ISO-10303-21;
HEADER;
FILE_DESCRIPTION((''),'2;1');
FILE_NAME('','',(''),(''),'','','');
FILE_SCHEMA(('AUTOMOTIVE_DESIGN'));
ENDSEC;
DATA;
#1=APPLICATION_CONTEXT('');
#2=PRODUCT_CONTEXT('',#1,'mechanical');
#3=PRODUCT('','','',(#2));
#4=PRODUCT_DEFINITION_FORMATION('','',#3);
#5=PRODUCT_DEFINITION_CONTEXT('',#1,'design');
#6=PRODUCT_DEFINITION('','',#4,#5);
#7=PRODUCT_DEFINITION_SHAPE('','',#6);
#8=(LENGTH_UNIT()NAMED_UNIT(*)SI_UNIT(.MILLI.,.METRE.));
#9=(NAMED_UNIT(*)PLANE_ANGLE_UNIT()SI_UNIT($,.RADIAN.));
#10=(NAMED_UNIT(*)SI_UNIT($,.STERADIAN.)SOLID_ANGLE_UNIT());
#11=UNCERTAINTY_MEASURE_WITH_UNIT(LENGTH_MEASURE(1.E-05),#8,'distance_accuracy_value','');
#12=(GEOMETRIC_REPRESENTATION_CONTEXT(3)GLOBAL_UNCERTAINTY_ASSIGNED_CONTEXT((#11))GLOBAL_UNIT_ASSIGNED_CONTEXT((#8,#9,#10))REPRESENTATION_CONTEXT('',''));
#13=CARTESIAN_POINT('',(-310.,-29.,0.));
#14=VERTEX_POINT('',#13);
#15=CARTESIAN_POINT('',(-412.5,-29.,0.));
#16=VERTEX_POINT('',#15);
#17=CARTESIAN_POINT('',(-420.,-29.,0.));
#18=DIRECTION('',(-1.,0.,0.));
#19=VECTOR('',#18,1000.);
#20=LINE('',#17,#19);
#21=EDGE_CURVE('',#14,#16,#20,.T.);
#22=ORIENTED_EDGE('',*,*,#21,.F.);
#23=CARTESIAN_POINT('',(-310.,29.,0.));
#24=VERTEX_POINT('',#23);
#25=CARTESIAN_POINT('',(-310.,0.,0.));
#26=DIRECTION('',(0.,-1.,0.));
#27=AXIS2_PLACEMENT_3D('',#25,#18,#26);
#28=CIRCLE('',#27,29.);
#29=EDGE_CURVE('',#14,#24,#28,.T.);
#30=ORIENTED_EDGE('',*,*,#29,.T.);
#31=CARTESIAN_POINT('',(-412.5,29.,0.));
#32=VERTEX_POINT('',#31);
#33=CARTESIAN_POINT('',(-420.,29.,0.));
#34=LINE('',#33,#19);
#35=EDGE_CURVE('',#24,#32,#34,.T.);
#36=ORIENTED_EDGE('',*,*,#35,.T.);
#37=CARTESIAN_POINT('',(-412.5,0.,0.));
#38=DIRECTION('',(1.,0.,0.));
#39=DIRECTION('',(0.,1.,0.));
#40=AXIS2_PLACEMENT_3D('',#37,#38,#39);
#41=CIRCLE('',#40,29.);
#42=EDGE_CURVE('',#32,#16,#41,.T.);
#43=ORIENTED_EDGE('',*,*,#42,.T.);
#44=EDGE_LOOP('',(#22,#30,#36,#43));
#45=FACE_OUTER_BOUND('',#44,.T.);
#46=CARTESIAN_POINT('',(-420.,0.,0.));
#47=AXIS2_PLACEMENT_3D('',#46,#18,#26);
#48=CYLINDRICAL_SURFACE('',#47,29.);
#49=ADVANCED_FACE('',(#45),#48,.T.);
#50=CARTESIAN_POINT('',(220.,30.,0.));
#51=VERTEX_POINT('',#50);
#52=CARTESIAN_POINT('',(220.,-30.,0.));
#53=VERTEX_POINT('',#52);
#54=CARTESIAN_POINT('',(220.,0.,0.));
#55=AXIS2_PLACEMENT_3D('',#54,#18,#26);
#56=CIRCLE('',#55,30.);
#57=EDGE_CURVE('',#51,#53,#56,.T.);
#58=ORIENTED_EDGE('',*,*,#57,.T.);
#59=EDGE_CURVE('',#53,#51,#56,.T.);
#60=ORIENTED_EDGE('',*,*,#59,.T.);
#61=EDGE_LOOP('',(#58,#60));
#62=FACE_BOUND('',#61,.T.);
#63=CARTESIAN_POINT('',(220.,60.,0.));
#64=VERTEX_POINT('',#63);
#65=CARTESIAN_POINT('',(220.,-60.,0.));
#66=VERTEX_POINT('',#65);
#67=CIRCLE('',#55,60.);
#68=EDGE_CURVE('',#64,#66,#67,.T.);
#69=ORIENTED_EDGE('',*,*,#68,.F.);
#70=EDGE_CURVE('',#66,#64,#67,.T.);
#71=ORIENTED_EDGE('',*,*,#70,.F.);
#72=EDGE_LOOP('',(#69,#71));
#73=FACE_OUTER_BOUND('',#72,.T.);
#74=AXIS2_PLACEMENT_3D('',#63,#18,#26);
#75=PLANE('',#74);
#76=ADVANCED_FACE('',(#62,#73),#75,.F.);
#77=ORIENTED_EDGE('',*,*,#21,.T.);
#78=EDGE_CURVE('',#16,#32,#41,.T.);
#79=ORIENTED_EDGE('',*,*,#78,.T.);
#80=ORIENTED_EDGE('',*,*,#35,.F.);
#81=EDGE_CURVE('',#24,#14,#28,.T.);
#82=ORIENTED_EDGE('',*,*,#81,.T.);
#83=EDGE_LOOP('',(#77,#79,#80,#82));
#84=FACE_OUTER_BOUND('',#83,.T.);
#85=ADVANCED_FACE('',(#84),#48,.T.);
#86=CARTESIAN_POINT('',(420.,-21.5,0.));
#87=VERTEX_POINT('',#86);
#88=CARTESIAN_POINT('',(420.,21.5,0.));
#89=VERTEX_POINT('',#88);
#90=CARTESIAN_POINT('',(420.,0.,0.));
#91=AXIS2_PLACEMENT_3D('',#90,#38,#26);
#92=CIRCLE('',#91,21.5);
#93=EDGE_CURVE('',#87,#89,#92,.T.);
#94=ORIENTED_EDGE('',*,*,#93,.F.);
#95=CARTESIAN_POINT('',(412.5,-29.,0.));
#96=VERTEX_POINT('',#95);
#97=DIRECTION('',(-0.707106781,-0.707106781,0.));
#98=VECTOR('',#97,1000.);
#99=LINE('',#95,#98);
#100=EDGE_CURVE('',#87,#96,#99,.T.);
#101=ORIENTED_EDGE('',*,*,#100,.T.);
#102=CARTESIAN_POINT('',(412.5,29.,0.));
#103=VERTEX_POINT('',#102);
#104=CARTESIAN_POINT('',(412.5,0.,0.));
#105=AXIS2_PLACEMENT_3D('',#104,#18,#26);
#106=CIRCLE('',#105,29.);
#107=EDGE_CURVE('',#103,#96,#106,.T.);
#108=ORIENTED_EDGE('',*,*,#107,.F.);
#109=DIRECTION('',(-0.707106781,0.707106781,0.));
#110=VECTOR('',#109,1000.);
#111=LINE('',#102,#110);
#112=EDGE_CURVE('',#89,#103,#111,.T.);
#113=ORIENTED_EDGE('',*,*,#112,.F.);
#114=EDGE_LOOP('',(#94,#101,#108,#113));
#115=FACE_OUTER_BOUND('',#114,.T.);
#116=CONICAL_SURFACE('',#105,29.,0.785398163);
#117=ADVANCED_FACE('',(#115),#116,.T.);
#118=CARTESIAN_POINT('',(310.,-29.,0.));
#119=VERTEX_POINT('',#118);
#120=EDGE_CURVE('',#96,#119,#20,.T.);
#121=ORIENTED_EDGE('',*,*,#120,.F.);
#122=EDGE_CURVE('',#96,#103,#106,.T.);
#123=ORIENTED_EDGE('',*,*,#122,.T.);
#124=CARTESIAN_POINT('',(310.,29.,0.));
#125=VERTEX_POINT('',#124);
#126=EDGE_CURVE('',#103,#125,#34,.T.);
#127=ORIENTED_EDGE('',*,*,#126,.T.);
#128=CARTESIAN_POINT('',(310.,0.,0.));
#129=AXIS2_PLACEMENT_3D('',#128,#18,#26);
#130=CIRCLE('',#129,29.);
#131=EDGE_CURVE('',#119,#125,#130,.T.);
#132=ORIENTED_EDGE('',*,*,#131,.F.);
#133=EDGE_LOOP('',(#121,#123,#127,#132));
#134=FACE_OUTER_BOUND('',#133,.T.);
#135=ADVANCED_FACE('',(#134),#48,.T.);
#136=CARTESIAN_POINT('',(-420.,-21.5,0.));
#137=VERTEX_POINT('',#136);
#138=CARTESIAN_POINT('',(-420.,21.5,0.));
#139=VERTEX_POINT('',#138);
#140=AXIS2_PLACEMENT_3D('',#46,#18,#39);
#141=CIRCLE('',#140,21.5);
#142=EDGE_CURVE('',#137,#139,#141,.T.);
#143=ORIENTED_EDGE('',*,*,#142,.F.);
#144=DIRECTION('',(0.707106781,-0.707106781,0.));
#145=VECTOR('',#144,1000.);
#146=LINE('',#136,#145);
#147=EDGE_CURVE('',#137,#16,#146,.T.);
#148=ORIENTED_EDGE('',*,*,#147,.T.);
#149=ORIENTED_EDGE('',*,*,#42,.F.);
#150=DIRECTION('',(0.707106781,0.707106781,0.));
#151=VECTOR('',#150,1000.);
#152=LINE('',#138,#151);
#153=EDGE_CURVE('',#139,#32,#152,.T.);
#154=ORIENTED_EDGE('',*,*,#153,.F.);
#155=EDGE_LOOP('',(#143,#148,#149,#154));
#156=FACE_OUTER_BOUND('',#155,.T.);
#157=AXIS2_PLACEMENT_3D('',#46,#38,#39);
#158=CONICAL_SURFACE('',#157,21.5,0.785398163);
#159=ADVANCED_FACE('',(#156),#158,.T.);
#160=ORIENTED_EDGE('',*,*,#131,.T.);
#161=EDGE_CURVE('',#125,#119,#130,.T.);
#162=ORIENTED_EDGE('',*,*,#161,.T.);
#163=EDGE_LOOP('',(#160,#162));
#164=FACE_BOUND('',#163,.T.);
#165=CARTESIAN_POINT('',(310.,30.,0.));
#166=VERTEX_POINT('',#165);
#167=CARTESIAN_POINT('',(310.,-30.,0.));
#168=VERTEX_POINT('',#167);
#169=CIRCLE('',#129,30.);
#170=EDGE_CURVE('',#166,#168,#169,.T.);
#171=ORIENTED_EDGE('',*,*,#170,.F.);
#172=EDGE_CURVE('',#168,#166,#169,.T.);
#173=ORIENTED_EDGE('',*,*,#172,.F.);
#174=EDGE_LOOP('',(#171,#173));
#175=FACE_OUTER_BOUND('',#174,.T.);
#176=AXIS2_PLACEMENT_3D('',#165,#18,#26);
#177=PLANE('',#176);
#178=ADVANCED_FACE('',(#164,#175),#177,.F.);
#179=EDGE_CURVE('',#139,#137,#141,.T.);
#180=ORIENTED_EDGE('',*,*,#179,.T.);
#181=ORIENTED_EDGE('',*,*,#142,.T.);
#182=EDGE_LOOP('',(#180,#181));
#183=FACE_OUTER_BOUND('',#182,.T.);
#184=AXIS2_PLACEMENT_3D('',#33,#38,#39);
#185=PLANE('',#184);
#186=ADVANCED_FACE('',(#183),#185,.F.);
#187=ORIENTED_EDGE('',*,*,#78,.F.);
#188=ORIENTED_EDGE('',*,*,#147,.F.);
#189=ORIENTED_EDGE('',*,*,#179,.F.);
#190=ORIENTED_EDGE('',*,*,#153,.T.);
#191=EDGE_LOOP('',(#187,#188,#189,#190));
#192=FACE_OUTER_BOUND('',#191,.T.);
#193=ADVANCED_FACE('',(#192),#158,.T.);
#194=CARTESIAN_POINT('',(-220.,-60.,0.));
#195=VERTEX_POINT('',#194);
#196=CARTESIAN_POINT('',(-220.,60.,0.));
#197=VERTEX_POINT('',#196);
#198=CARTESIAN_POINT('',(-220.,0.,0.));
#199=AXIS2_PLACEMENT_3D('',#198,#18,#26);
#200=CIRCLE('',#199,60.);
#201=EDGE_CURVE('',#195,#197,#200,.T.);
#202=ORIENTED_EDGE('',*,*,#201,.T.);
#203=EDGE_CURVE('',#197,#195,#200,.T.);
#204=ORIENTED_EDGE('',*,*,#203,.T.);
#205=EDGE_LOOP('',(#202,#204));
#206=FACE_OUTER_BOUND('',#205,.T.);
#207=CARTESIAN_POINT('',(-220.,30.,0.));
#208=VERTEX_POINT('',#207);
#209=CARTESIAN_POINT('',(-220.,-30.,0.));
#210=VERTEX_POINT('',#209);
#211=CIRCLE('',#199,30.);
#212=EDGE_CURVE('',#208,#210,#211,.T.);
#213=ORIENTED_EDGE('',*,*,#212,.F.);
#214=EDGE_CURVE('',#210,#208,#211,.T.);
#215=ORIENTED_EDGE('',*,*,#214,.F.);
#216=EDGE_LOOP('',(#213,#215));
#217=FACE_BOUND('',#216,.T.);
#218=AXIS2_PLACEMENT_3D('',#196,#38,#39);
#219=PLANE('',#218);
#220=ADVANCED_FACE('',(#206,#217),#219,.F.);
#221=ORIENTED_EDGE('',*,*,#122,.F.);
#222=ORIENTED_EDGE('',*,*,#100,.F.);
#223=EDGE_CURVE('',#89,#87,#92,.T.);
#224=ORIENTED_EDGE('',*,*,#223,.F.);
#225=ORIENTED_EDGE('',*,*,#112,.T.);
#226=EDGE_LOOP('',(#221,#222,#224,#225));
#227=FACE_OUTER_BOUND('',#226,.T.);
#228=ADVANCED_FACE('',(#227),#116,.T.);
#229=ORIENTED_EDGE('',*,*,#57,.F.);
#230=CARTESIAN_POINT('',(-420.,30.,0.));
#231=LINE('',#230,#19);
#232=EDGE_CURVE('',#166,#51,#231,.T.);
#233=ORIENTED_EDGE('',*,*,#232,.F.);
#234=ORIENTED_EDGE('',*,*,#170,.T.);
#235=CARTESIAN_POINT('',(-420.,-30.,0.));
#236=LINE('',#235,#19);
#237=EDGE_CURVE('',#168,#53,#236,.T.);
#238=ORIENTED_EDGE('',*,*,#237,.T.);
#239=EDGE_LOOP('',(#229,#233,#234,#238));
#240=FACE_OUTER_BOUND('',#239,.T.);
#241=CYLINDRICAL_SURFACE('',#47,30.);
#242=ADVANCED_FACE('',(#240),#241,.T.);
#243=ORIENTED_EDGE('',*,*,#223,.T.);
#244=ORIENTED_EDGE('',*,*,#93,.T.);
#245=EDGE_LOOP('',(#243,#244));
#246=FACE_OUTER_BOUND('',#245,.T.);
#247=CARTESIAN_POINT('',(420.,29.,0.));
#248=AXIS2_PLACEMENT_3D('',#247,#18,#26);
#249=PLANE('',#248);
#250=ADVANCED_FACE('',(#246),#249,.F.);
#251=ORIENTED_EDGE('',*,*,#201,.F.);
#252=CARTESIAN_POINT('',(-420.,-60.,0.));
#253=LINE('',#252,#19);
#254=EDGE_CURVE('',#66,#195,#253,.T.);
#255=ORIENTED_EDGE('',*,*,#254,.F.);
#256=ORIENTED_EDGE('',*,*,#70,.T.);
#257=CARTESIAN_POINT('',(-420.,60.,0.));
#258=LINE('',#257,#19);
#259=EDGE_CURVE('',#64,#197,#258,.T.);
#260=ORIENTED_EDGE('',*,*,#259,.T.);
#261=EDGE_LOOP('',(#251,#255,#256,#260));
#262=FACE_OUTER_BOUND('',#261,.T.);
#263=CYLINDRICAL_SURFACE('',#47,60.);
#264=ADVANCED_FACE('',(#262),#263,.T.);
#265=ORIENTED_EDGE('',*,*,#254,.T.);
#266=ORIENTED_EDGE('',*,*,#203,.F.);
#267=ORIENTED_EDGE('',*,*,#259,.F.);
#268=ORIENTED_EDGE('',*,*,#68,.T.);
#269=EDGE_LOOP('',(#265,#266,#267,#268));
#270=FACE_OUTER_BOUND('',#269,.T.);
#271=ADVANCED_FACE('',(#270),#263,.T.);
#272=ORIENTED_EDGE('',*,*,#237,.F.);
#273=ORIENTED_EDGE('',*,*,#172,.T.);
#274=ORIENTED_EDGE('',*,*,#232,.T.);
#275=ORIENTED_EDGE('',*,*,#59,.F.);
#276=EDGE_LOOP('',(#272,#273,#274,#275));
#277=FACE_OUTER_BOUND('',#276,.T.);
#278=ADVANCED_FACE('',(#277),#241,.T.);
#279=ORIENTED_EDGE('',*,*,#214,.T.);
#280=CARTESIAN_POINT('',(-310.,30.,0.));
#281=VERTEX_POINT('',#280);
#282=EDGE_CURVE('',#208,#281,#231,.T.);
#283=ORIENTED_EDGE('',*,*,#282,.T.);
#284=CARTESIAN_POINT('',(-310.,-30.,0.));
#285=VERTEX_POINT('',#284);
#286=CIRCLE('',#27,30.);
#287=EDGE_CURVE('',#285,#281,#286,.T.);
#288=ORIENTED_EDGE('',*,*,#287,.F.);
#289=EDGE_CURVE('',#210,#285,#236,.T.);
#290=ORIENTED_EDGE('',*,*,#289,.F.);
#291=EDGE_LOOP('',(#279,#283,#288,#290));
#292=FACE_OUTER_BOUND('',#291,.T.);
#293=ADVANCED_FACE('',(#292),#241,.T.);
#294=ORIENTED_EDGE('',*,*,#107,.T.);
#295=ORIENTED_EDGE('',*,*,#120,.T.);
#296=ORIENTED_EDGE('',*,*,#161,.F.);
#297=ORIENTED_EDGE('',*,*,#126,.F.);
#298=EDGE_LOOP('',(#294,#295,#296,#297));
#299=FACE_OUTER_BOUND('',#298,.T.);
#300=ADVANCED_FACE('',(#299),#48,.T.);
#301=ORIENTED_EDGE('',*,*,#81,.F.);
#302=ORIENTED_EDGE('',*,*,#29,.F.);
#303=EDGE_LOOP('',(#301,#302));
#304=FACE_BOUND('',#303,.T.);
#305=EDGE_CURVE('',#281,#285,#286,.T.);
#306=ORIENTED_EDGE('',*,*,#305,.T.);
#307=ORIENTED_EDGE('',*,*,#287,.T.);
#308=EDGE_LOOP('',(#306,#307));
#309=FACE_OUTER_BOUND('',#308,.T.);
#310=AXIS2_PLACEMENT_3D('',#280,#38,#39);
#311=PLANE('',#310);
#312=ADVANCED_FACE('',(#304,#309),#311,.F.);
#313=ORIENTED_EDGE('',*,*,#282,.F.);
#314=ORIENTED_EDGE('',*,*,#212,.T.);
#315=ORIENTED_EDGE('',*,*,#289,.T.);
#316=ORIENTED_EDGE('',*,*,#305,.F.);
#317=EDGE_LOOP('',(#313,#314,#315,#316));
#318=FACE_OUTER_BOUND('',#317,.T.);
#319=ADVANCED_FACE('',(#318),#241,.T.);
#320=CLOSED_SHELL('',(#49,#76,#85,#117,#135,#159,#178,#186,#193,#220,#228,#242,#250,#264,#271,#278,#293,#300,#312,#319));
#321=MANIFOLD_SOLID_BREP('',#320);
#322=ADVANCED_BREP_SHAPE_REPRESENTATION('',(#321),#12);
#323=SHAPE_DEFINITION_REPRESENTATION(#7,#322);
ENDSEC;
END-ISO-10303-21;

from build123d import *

# Parameters (mm, degrees)
END_CHAMFER_7_5X45_SIZE = 7.5


with BuildPart() as part:
    # Shaft Profile Sketch → Stepped Shaft Body (revolve)
    with BuildSketch(Plane.XY, mode=Mode.PRIVATE) as stepped_shaft_body_sk:
        Polygon((220, 60), (-220, 60), (-220, 30), (-310, 30), (-310, 29), (-420, 29), (-420, 0), (420, 0), (420, 29), (310, 29), (310, 30), (220, 30), align=None)
    revolve(stepped_shaft_body_sk.sketch.rotate(Axis((-420, 0, 0), (1, 0, 0)), 180), axis=Axis((-420, 0, 0), (1, 0, 0)))

    # End Chamfer 7.5x45°
    end_chamfer_7_5x45_edges = [part.edges().sort_by_distance(p)[0] for p in [
        (-420, 29, 0),
        (420, 29, 0),
    ]]
    chamfer(end_chamfer_7_5x45_edges, length=END_CHAMFER_7_5X45_SIZE)


solid = part.part
